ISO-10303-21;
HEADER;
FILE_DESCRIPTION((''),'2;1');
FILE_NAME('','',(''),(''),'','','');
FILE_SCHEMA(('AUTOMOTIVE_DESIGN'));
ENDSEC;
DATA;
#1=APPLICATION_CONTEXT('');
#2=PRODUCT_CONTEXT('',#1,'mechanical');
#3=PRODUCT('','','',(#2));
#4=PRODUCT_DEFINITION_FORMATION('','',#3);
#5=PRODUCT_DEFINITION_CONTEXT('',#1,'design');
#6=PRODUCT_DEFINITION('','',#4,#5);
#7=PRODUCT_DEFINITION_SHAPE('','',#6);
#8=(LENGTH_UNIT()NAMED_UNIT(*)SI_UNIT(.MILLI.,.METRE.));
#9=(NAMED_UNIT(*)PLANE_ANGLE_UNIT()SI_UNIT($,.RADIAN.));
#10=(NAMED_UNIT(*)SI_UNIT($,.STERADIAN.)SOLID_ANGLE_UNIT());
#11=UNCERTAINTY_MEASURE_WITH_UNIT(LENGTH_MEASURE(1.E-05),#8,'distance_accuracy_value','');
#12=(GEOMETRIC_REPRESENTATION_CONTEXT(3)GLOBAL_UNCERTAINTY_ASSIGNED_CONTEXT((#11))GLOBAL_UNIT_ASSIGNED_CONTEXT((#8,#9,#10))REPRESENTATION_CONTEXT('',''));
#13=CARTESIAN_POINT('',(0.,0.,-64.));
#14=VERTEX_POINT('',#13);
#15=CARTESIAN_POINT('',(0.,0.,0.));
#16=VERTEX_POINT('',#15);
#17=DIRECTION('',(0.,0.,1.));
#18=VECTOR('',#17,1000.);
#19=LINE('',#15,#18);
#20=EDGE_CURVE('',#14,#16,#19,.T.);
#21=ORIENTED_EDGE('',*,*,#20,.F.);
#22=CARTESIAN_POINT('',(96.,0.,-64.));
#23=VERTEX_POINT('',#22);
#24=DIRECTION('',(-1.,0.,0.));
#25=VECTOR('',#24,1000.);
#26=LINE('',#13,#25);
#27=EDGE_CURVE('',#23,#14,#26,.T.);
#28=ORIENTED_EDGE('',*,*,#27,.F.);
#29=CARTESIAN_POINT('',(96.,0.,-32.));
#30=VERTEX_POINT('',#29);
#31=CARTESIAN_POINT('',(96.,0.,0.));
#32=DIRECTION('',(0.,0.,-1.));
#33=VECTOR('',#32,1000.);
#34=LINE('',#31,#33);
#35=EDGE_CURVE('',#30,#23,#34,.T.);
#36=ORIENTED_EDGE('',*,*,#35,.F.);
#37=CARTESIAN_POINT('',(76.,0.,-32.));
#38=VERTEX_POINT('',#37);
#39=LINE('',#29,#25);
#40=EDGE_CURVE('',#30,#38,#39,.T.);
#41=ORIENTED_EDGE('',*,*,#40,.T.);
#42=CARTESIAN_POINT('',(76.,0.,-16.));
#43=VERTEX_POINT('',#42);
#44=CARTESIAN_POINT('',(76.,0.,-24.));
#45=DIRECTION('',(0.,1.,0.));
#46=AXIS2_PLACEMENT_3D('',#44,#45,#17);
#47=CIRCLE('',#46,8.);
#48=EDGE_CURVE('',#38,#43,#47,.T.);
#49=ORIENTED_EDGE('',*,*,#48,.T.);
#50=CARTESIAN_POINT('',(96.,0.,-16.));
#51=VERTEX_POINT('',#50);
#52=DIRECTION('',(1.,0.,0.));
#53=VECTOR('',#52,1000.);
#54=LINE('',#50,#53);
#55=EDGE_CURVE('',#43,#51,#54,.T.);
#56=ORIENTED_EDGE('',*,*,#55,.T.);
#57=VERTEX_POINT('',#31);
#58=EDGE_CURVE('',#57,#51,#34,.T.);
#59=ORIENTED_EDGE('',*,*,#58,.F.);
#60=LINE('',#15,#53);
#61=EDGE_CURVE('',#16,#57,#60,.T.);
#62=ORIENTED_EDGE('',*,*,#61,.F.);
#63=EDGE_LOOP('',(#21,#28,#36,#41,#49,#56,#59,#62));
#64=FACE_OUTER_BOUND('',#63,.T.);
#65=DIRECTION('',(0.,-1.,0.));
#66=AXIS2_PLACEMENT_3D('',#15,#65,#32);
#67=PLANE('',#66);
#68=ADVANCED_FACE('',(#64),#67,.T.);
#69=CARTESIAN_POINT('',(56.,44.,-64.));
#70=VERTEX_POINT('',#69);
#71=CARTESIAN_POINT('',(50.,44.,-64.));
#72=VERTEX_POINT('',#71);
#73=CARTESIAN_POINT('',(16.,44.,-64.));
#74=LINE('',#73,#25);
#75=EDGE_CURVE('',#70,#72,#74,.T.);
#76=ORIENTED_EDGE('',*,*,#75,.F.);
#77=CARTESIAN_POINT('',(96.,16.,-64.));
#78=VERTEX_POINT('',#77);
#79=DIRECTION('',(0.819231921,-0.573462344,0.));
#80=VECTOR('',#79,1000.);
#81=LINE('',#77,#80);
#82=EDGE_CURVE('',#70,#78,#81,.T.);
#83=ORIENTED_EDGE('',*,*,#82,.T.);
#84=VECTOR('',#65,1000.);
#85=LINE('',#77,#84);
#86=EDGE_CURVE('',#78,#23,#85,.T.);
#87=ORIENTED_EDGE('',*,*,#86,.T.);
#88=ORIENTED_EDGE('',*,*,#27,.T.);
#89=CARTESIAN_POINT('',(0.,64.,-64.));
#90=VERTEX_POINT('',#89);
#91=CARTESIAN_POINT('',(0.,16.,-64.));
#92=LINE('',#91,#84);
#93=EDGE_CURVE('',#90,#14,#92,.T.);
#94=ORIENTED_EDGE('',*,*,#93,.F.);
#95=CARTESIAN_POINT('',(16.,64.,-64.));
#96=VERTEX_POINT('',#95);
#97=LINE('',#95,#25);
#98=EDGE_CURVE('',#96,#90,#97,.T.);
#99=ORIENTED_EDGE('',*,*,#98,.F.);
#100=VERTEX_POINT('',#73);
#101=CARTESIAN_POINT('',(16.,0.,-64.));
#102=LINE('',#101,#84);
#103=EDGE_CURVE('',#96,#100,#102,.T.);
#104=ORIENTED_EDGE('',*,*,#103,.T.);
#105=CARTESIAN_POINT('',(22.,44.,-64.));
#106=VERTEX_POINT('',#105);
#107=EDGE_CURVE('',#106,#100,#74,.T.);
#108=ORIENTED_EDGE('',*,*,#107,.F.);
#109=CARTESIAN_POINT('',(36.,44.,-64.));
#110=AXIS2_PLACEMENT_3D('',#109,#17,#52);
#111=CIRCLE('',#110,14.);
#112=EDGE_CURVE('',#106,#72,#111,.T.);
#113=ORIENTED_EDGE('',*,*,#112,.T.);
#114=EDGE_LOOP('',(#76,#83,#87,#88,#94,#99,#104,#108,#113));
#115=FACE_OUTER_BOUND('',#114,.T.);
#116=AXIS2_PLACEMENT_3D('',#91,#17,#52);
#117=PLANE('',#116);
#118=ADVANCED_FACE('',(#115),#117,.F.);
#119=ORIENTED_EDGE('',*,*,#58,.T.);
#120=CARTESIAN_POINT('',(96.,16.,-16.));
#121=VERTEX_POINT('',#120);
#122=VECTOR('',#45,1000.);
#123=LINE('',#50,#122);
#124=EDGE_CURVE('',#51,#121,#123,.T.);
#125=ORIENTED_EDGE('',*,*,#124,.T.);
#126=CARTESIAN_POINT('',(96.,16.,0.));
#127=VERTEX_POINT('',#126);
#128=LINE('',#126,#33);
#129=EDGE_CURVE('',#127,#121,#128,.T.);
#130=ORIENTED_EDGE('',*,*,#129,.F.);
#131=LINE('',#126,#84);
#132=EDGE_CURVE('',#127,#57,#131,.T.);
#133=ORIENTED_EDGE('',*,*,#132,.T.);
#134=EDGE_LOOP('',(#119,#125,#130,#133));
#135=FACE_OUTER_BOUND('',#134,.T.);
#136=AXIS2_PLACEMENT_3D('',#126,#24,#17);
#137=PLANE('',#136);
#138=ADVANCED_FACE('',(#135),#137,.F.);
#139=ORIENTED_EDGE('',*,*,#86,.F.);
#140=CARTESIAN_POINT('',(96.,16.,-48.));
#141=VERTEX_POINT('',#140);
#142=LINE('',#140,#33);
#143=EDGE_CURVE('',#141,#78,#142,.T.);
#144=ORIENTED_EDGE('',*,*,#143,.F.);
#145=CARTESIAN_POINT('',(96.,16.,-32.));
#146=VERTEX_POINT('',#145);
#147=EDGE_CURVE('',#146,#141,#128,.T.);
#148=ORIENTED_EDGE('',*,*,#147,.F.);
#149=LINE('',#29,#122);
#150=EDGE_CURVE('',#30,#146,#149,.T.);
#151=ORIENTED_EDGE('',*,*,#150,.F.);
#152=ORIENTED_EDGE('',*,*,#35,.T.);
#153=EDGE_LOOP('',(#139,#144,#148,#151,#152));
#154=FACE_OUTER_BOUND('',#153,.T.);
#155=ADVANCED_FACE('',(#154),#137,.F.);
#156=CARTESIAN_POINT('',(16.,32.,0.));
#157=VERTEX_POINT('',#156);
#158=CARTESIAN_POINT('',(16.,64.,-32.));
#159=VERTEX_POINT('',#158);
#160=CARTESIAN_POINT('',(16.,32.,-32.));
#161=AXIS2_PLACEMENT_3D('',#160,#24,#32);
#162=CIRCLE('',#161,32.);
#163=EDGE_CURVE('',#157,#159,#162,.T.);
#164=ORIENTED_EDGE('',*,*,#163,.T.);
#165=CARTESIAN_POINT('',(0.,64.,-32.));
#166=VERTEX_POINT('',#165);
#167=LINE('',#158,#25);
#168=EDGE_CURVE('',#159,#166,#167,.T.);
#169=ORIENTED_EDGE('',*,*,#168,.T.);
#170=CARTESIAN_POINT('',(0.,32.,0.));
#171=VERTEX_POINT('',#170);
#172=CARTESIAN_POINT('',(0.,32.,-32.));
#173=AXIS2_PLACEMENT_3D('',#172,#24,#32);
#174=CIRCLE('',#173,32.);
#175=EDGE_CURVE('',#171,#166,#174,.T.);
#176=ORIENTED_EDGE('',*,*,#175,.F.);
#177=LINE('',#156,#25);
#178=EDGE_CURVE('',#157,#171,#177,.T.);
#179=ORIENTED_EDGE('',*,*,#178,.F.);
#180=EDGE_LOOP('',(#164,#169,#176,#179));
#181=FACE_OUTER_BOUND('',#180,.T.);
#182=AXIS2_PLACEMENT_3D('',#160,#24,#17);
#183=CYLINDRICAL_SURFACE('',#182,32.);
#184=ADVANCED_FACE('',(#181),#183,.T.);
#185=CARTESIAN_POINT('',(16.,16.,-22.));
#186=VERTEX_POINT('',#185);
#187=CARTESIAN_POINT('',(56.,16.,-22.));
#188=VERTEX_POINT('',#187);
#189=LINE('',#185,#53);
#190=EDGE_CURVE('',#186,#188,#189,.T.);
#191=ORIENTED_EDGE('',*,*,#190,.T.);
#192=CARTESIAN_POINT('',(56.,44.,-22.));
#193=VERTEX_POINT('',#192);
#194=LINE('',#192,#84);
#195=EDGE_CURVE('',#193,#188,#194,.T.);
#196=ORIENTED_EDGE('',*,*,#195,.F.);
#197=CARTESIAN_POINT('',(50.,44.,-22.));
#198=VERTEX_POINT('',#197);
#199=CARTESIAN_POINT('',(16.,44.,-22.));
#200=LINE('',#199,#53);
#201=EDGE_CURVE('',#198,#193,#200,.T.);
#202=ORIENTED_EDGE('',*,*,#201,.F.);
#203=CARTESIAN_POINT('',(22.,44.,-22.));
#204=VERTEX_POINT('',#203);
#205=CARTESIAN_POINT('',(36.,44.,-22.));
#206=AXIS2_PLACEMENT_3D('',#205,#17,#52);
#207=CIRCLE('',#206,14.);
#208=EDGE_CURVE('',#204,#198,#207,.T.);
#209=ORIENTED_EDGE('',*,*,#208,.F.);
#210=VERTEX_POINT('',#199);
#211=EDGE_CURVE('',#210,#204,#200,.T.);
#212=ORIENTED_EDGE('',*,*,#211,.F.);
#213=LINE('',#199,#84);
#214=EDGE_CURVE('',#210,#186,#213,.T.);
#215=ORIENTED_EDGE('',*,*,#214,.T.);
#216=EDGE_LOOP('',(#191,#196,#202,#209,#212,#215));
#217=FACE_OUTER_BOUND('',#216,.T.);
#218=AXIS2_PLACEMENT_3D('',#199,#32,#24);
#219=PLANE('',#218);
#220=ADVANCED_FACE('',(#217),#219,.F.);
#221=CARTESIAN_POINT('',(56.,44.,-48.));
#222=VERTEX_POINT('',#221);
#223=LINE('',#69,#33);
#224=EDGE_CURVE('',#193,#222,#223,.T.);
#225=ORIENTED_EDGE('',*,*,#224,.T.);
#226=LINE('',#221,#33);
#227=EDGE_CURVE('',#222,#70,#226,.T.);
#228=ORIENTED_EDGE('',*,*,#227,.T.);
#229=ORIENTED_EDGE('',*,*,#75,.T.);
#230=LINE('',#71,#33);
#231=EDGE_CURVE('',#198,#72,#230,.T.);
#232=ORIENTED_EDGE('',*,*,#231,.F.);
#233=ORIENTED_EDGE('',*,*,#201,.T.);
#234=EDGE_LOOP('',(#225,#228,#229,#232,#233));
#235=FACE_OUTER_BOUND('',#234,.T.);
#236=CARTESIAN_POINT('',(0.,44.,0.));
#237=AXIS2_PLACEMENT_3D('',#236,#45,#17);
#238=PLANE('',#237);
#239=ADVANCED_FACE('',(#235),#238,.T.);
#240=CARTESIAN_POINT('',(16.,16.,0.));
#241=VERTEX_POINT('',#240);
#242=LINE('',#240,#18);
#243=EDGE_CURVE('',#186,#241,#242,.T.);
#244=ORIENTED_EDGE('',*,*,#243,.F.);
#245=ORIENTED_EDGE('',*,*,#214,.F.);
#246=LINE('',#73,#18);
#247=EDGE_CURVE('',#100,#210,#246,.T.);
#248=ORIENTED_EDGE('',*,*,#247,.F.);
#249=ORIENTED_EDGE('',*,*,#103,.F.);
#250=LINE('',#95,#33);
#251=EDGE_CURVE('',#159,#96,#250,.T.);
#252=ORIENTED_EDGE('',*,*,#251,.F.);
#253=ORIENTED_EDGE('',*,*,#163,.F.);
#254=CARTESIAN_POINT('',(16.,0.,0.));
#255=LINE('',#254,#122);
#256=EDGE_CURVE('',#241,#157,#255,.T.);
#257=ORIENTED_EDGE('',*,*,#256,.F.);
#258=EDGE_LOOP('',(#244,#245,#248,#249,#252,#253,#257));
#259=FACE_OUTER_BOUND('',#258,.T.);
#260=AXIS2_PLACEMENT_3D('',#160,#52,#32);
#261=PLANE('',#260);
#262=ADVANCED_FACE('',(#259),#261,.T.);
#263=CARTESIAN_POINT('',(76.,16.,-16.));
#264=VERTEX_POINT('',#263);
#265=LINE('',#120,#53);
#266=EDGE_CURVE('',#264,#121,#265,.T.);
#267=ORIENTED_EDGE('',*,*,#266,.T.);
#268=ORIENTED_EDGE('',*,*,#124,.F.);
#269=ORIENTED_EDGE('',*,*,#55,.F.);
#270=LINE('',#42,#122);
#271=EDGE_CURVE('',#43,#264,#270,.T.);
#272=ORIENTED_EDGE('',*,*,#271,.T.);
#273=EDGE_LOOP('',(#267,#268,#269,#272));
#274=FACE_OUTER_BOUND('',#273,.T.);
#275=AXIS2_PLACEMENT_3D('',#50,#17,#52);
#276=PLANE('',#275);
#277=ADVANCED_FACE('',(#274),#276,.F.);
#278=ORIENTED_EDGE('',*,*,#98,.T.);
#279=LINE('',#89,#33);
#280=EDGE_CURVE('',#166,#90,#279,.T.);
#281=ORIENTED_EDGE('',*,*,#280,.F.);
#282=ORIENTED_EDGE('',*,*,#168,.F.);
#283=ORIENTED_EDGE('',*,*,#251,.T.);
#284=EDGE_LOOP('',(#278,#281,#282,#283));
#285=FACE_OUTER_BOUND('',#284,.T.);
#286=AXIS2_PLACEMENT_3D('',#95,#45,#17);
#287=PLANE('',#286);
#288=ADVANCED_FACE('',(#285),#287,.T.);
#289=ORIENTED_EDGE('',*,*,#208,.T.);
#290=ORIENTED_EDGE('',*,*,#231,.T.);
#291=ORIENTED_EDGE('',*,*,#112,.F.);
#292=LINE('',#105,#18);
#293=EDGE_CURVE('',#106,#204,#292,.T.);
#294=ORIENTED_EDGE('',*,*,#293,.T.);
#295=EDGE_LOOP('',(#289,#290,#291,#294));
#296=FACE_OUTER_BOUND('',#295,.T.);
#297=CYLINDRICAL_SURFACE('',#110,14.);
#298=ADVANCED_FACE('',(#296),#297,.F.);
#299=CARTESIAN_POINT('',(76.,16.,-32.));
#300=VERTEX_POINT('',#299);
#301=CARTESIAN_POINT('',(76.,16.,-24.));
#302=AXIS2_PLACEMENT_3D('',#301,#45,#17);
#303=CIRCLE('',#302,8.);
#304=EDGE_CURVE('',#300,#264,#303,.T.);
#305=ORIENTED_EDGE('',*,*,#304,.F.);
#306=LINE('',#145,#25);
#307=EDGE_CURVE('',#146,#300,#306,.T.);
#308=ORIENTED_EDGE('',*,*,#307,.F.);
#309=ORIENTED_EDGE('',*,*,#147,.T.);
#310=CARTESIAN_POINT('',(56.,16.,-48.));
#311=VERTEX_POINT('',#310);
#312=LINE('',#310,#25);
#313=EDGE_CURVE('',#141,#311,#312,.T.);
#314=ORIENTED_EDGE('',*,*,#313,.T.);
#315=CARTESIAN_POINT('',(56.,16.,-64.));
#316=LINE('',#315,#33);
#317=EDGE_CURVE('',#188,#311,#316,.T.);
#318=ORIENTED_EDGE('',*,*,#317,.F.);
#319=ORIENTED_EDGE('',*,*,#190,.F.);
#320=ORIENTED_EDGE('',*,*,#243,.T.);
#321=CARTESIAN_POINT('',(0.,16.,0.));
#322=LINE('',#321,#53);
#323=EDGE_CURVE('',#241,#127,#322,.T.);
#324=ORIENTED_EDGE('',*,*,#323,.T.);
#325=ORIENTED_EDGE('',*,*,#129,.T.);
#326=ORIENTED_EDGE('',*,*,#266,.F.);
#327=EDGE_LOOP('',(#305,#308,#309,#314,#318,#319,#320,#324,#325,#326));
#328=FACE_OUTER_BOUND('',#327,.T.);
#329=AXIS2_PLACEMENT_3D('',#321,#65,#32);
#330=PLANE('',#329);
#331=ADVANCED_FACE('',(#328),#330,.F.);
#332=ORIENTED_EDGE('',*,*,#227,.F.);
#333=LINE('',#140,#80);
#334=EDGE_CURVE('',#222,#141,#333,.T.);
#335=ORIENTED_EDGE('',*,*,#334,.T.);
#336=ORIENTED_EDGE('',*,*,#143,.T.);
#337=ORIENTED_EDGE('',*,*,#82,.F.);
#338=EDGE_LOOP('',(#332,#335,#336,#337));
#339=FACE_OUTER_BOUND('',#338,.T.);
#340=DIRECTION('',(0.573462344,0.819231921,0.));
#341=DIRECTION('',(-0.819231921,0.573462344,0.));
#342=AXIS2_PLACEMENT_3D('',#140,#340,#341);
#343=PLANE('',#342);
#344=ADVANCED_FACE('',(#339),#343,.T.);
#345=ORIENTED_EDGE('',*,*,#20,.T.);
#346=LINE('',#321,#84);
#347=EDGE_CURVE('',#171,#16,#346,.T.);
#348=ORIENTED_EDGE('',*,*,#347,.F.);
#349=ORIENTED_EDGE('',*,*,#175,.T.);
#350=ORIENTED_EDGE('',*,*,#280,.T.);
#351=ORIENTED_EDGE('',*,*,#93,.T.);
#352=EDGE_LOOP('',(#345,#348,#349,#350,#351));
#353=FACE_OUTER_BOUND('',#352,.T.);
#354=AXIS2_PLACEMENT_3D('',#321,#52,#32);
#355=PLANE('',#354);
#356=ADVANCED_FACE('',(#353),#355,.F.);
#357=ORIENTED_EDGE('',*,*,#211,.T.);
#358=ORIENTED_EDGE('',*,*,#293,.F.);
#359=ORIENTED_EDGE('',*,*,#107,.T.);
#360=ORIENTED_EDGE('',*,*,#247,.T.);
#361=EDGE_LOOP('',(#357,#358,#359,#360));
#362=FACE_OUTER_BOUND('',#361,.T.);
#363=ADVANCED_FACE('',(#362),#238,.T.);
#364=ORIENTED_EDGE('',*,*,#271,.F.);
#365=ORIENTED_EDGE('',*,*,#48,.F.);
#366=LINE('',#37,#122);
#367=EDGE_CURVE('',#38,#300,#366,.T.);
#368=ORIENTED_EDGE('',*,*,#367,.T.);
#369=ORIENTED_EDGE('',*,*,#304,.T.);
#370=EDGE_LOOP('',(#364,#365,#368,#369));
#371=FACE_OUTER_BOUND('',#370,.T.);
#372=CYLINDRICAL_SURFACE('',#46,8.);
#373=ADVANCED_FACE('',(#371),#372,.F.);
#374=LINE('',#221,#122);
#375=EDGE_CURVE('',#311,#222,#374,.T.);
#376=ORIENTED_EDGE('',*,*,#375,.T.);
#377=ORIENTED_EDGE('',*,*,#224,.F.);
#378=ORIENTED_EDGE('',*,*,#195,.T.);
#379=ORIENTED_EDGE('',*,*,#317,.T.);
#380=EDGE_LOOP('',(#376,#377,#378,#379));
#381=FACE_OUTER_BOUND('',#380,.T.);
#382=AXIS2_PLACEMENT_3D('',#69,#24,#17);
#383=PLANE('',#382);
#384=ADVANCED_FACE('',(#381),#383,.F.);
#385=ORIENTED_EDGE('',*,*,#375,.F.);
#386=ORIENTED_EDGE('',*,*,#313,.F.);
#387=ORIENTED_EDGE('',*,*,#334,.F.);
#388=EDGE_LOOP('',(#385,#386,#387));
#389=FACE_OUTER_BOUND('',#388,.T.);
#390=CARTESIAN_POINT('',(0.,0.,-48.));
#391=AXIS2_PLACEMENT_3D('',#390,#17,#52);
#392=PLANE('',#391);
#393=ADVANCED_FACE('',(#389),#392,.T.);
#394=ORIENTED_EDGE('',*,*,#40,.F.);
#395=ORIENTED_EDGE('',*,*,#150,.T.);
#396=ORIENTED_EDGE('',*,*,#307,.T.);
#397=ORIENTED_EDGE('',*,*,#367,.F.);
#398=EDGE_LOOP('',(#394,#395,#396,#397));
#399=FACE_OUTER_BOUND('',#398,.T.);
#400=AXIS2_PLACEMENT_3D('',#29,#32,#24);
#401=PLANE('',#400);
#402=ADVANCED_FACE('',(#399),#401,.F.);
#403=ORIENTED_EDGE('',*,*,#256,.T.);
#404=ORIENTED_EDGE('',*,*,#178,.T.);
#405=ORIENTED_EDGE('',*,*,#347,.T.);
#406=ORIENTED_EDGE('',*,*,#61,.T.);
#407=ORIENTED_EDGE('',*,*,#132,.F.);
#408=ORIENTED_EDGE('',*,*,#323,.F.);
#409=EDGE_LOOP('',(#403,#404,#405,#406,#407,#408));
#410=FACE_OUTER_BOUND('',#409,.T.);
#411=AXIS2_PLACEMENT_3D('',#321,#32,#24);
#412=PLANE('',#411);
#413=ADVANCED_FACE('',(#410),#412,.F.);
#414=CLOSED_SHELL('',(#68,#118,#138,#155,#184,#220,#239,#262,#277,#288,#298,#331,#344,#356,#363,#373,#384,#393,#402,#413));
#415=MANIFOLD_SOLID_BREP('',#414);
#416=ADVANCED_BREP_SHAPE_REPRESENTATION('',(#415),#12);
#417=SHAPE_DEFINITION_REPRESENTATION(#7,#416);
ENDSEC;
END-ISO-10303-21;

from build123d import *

# Parameters (mm, degrees)
BASE_PLATE_SKETCH_W         = 96
BASE_PLATE_SKETCH_H         = 64
BASE_PLATE_96X64X16_DEPTH   = 16
U_SLOT_DEPTH                = 16
UPRIGHT_R32_DEPTH           = 16
CRADLE_BLOCK_SKETCH_W       = 40
CRADLE_BLOCK_SKETCH_H       = 42
CRADLE_BLOCK_40X22X28_DEPTH = 28
CRADLE_BORE_SKETCH_R        = 14
CRADLE_BORE_28_DEPTH        = 123.784363825
GUSSET_RIB_DEPTH            = 16


with BuildPart() as part:
    # Base Plate Sketch → Base Plate 96x64x16 (new body)
    with BuildSketch(Plane(origin=(0, 0, 0), x_dir=(1, 0, 0), z_dir=(0, 1, 0))):
        with Locations((48, 32)):
            Rectangle(BASE_PLATE_SKETCH_W, BASE_PLATE_SKETCH_H)
    extrude(amount=BASE_PLATE_96X64X16_DEPTH)

    # U-Slot Sketch → U-Slot (cut)
    with BuildSketch(Plane(origin=(0, 16, 0), x_dir=(1, 0, 0), z_dir=(0, 1, 0))):
        with BuildLine():
            Line((96, 16), (76, 16))
            ThreePointArc((76, 16), (68, 24), (76, 32))
            Line((76, 32), (96, 32))
            ThreePointArc((96, 32), (104, 24), (96, 16))
        make_face()
    extrude(amount=-U_SLOT_DEPTH, mode=Mode.SUBTRACT)

    # Upright Sketch → Upright R32 (add)
    with BuildSketch(Plane.ZY):
        with BuildLine():
            Line((-64, 0), (0, 0))
            Line((0, 0), (0, 32))
            ThreePointArc((0, 32), (-9.372583002, 54.627416998), (-32, 64))
            Line((-32, 64), (-64, 64))
            Line((-64, 64), (-64, 0))
        make_face()
    extrude(amount=-UPRIGHT_R32_DEPTH)

    # Cradle Block Sketch → Cradle Block 40x22x28 (add)
    with BuildSketch(Plane(origin=(0, 16, 0), x_dir=(1, 0, 0), z_dir=(0, 1, 0))):
        with Locations((36, 43)):
            Rectangle(CRADLE_BLOCK_SKETCH_W, CRADLE_BLOCK_SKETCH_H)
    extrude(amount=CRADLE_BLOCK_40X22X28_DEPTH)

    # Cradle Bore Sketch → Cradle Bore Ø28 (cut, through all)
    with BuildSketch(Plane.XY.offset(-22)):
        with Locations((36, 44)):
            Circle(CRADLE_BORE_SKETCH_R)
    extrude(amount=-CRADLE_BORE_28_DEPTH, mode=Mode.SUBTRACT)

    # Gusset Rib Sketch → Gusset Rib (add)
    with BuildSketch(Plane(origin=(0, 0, -64), x_dir=(-1, 0, 0), z_dir=(0, 0, -1))):
        Polygon((-56, 44), (-56, 16), (-96, 16), align=None)
    extrude(amount=-GUSSET_RIB_DEPTH)


solid = part.part
